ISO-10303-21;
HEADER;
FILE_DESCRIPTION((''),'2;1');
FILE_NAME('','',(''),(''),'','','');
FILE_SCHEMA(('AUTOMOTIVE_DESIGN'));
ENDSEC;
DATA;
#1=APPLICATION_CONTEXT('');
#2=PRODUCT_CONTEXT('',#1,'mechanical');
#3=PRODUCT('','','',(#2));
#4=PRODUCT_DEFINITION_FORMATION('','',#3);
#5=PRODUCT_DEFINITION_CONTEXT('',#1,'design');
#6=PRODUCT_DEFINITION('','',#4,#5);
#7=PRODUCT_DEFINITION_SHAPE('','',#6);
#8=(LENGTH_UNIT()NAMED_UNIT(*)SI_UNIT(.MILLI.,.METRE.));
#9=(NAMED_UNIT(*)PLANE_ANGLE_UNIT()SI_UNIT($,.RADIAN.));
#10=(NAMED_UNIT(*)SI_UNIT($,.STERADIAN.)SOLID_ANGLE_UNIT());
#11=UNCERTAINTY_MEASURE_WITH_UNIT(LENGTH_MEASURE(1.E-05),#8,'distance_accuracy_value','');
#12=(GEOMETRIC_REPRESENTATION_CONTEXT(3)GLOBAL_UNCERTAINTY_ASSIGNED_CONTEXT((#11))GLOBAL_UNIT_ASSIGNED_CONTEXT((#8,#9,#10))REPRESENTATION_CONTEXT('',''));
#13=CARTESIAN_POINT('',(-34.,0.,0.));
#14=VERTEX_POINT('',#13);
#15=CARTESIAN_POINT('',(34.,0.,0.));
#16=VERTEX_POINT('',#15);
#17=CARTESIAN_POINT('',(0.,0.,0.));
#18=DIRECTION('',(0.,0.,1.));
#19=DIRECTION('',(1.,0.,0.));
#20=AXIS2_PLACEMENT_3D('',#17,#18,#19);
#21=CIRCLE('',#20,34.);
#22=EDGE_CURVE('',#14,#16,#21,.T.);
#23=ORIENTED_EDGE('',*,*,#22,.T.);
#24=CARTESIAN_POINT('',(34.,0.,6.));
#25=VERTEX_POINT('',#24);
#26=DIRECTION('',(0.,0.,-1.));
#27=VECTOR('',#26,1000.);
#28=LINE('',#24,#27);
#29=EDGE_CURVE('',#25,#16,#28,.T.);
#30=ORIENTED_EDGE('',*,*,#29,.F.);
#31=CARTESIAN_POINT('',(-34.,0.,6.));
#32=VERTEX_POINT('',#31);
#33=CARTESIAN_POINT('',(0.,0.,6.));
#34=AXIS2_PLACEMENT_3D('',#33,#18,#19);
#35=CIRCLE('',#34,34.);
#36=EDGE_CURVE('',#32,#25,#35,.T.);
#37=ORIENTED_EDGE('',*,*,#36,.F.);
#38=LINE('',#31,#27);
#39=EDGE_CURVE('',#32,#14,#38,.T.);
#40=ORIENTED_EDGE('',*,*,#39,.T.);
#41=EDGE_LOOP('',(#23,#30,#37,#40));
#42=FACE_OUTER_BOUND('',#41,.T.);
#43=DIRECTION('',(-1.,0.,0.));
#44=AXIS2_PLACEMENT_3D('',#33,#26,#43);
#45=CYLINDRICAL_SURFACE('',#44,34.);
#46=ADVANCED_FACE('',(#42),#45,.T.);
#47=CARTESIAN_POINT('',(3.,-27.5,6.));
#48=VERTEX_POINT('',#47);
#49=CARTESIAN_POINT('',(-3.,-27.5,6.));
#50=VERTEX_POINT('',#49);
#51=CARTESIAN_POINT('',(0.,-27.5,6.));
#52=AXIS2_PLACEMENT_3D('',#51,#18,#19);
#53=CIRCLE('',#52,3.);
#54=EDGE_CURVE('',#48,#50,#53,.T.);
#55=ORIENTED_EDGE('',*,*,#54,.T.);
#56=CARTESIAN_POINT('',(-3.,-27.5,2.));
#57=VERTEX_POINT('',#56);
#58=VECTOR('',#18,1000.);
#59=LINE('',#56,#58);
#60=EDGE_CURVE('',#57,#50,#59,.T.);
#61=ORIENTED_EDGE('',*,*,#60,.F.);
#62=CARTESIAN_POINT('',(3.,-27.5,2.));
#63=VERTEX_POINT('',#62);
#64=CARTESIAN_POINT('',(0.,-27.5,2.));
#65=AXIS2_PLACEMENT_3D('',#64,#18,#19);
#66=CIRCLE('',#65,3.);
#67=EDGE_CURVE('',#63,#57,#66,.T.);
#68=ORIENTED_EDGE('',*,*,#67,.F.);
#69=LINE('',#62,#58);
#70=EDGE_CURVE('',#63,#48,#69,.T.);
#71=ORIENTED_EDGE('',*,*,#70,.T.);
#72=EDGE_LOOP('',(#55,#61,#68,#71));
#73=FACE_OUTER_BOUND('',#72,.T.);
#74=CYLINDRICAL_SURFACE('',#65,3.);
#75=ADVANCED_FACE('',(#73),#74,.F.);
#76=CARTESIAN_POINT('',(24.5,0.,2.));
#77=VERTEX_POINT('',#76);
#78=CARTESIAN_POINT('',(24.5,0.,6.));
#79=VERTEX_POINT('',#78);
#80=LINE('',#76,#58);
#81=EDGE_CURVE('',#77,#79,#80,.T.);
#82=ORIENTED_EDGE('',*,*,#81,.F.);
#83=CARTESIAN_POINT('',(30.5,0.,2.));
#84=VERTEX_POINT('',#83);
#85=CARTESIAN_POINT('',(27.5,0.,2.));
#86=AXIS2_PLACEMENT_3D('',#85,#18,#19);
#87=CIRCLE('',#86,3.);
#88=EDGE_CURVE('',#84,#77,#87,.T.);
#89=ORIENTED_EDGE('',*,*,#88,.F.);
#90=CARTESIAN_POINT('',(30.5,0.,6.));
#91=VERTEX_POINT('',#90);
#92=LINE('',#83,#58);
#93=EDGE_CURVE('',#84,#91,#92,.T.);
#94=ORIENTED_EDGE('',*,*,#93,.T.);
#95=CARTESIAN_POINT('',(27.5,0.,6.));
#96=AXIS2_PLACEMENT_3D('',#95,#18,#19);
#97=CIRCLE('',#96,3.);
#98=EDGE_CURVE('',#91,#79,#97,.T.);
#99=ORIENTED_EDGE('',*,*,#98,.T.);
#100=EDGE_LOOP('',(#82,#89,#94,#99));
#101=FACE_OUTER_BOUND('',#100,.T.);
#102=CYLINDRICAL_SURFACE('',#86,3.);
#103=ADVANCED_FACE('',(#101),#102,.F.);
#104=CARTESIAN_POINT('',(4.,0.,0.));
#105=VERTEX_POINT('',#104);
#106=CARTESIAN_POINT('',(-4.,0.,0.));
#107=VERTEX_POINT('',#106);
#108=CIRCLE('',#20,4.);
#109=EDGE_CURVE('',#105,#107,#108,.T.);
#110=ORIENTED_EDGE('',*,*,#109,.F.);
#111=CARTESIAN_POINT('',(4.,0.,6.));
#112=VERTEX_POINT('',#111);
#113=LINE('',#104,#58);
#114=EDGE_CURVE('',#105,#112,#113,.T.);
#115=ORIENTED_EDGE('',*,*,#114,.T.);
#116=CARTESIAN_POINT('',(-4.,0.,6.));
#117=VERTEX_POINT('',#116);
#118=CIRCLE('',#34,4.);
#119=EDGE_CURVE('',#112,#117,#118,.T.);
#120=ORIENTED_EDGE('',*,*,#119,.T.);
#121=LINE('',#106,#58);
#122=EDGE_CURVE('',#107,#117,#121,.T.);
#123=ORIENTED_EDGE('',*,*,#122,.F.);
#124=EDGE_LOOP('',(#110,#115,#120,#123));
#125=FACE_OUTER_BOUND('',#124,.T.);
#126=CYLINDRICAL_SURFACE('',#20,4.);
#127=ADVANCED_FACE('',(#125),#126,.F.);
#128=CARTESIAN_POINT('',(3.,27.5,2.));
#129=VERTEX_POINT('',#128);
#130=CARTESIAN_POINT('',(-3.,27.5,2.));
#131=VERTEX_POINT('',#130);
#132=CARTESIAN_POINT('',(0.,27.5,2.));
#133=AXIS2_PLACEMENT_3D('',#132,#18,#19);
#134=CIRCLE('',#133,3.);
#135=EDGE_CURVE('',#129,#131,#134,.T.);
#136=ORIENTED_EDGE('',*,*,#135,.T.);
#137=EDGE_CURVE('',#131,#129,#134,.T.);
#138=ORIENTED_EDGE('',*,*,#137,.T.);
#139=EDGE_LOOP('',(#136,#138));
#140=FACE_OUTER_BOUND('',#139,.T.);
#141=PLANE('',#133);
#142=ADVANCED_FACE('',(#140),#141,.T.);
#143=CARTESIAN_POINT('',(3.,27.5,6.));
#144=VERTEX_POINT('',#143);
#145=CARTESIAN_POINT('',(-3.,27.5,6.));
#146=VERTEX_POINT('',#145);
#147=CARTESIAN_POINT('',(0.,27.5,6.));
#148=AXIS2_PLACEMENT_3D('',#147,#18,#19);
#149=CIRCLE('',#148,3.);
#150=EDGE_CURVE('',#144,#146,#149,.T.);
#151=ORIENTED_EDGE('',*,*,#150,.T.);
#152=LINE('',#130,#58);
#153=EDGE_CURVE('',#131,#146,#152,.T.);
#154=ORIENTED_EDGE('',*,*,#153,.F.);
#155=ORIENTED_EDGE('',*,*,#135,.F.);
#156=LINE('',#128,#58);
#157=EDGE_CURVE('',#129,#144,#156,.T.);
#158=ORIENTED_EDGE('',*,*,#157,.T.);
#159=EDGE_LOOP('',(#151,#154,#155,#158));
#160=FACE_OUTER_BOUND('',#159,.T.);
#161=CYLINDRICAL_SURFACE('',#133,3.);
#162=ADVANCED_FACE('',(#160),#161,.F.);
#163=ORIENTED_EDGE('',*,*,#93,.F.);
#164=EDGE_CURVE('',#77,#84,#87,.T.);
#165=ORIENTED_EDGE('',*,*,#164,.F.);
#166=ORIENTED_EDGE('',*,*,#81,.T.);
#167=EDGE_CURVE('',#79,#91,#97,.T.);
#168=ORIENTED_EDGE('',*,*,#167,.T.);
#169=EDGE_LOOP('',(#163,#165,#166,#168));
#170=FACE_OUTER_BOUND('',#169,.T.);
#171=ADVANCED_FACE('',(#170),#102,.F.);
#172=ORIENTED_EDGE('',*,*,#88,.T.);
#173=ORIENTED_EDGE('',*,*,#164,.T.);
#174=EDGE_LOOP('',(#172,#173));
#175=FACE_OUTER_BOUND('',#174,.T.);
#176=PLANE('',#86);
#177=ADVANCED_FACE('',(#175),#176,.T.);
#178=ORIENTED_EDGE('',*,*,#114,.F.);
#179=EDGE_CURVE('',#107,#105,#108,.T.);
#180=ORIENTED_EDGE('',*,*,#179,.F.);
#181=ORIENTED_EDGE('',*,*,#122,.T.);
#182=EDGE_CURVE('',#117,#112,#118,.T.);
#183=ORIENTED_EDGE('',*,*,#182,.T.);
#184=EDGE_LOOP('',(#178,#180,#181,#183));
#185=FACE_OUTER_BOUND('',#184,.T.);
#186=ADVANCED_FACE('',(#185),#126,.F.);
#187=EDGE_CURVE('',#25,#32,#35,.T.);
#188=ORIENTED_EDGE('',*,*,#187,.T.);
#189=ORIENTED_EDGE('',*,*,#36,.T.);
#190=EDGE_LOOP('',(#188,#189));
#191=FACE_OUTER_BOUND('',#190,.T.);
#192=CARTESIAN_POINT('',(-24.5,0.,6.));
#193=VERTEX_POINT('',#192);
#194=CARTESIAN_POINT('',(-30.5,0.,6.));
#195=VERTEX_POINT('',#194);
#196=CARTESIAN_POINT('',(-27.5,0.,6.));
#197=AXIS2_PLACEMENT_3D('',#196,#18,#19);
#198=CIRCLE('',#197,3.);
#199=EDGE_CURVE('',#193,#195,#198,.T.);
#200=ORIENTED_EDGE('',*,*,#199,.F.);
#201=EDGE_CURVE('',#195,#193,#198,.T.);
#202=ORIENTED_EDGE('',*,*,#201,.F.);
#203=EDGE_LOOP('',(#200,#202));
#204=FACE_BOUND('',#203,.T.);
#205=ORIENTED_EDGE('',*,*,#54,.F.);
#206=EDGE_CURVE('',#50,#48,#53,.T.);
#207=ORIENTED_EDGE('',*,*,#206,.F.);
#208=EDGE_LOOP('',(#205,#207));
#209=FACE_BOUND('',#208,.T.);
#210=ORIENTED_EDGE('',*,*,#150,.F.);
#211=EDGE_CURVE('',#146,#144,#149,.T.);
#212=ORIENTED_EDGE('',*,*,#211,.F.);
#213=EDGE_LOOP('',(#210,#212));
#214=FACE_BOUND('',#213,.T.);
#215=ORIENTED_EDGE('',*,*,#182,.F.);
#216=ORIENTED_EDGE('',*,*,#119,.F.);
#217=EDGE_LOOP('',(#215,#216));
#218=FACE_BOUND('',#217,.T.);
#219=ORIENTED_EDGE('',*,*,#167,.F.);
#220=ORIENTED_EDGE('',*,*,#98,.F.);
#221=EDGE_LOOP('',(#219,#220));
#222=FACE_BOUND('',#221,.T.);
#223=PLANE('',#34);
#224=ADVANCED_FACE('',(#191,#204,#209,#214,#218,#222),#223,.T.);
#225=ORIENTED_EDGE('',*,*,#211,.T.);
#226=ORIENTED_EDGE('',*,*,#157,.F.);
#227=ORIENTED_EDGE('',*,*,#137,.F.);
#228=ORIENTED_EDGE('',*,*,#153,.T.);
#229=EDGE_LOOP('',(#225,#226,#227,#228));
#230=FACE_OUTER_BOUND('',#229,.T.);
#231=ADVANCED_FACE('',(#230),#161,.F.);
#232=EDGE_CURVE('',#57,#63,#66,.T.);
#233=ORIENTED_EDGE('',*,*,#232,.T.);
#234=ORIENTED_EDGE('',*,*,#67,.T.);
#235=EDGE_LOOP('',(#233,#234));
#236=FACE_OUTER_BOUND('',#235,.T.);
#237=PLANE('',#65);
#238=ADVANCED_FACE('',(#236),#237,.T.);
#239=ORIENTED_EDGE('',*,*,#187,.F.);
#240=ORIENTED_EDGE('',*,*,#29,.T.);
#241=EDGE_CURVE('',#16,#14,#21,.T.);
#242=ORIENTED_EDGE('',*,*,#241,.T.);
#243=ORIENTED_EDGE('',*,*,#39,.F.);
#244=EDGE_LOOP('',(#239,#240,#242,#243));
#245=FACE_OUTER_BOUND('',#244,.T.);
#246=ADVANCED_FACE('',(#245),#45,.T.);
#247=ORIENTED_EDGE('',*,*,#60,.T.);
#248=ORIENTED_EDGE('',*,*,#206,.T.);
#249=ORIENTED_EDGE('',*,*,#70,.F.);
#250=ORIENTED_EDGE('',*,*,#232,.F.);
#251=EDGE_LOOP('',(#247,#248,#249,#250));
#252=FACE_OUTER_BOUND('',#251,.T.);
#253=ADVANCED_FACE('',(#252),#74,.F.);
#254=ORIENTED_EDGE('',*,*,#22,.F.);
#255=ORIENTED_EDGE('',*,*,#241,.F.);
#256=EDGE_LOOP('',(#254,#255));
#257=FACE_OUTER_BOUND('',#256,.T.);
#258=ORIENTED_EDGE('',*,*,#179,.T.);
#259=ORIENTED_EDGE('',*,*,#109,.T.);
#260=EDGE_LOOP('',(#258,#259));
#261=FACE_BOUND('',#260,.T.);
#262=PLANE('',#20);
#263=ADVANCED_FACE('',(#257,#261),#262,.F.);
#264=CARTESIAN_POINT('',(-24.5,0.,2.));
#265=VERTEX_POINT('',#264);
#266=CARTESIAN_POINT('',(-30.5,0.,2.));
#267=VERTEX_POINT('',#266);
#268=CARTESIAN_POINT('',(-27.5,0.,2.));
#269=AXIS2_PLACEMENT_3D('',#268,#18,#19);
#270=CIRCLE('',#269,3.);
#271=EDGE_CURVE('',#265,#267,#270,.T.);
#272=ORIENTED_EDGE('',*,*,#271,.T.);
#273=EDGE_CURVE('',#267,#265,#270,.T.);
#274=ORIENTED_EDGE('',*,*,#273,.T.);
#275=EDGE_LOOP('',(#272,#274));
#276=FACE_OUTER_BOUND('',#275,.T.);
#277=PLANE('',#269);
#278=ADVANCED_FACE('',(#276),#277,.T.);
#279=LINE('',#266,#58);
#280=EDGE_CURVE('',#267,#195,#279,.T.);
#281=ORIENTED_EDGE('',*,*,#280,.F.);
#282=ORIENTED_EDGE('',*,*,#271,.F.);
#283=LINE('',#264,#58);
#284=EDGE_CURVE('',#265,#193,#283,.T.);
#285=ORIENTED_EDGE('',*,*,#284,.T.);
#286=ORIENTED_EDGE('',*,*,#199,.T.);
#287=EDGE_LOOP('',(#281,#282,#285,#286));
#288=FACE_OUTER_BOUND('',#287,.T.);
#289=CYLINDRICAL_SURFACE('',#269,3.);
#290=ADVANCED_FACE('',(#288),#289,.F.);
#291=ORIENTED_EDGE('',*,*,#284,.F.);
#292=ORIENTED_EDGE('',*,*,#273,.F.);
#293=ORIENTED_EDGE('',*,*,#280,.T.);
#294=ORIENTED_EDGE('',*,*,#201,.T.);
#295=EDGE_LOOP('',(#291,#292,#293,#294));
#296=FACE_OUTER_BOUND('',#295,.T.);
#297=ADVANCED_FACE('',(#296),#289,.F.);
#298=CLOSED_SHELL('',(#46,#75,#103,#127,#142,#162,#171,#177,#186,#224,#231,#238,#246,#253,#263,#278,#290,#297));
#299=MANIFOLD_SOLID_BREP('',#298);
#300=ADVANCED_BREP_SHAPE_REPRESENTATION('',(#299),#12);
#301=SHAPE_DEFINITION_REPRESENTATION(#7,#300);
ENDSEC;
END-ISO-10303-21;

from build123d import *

# Parameters (mm, degrees)
SKETCH1_R           = 34
BOSS_EXTRUDE1_DEPTH = 6
SKETCH2_R           = 3
CUT_EXTRUDE1_DEPTH  = 4
SKETCH3_R           = 4
CUT_EXTRUDE2_DEPTH  = 49.456165758


with BuildPart() as part:
    # Sketch1 → Boss-Extrude1 (new body)
    with BuildSketch(Plane.XY):
        Circle(SKETCH1_R)
    extrude(amount=BOSS_EXTRUDE1_DEPTH)

    # Sketch2 → Cut-Extrude1 (cut)
    with BuildSketch(Plane.XY.offset(6)):
        with Locations((0, 27.5)):
            Circle(SKETCH2_R)
        with Locations((27.5, 0)):
            Circle(SKETCH2_R)
        with Locations((0, -27.5)):
            Circle(SKETCH2_R)
        with Locations((-27.5, 0)):
            Circle(SKETCH2_R)
    extrude(amount=-CUT_EXTRUDE1_DEPTH, mode=Mode.SUBTRACT)

    # Sketch3 → Cut-Extrude2 (cut, through all)
    with BuildSketch(Plane.XY.offset(6)):
        Circle(SKETCH3_R)
    extrude(amount=-CUT_EXTRUDE2_DEPTH, mode=Mode.SUBTRACT)


solid = part.part
